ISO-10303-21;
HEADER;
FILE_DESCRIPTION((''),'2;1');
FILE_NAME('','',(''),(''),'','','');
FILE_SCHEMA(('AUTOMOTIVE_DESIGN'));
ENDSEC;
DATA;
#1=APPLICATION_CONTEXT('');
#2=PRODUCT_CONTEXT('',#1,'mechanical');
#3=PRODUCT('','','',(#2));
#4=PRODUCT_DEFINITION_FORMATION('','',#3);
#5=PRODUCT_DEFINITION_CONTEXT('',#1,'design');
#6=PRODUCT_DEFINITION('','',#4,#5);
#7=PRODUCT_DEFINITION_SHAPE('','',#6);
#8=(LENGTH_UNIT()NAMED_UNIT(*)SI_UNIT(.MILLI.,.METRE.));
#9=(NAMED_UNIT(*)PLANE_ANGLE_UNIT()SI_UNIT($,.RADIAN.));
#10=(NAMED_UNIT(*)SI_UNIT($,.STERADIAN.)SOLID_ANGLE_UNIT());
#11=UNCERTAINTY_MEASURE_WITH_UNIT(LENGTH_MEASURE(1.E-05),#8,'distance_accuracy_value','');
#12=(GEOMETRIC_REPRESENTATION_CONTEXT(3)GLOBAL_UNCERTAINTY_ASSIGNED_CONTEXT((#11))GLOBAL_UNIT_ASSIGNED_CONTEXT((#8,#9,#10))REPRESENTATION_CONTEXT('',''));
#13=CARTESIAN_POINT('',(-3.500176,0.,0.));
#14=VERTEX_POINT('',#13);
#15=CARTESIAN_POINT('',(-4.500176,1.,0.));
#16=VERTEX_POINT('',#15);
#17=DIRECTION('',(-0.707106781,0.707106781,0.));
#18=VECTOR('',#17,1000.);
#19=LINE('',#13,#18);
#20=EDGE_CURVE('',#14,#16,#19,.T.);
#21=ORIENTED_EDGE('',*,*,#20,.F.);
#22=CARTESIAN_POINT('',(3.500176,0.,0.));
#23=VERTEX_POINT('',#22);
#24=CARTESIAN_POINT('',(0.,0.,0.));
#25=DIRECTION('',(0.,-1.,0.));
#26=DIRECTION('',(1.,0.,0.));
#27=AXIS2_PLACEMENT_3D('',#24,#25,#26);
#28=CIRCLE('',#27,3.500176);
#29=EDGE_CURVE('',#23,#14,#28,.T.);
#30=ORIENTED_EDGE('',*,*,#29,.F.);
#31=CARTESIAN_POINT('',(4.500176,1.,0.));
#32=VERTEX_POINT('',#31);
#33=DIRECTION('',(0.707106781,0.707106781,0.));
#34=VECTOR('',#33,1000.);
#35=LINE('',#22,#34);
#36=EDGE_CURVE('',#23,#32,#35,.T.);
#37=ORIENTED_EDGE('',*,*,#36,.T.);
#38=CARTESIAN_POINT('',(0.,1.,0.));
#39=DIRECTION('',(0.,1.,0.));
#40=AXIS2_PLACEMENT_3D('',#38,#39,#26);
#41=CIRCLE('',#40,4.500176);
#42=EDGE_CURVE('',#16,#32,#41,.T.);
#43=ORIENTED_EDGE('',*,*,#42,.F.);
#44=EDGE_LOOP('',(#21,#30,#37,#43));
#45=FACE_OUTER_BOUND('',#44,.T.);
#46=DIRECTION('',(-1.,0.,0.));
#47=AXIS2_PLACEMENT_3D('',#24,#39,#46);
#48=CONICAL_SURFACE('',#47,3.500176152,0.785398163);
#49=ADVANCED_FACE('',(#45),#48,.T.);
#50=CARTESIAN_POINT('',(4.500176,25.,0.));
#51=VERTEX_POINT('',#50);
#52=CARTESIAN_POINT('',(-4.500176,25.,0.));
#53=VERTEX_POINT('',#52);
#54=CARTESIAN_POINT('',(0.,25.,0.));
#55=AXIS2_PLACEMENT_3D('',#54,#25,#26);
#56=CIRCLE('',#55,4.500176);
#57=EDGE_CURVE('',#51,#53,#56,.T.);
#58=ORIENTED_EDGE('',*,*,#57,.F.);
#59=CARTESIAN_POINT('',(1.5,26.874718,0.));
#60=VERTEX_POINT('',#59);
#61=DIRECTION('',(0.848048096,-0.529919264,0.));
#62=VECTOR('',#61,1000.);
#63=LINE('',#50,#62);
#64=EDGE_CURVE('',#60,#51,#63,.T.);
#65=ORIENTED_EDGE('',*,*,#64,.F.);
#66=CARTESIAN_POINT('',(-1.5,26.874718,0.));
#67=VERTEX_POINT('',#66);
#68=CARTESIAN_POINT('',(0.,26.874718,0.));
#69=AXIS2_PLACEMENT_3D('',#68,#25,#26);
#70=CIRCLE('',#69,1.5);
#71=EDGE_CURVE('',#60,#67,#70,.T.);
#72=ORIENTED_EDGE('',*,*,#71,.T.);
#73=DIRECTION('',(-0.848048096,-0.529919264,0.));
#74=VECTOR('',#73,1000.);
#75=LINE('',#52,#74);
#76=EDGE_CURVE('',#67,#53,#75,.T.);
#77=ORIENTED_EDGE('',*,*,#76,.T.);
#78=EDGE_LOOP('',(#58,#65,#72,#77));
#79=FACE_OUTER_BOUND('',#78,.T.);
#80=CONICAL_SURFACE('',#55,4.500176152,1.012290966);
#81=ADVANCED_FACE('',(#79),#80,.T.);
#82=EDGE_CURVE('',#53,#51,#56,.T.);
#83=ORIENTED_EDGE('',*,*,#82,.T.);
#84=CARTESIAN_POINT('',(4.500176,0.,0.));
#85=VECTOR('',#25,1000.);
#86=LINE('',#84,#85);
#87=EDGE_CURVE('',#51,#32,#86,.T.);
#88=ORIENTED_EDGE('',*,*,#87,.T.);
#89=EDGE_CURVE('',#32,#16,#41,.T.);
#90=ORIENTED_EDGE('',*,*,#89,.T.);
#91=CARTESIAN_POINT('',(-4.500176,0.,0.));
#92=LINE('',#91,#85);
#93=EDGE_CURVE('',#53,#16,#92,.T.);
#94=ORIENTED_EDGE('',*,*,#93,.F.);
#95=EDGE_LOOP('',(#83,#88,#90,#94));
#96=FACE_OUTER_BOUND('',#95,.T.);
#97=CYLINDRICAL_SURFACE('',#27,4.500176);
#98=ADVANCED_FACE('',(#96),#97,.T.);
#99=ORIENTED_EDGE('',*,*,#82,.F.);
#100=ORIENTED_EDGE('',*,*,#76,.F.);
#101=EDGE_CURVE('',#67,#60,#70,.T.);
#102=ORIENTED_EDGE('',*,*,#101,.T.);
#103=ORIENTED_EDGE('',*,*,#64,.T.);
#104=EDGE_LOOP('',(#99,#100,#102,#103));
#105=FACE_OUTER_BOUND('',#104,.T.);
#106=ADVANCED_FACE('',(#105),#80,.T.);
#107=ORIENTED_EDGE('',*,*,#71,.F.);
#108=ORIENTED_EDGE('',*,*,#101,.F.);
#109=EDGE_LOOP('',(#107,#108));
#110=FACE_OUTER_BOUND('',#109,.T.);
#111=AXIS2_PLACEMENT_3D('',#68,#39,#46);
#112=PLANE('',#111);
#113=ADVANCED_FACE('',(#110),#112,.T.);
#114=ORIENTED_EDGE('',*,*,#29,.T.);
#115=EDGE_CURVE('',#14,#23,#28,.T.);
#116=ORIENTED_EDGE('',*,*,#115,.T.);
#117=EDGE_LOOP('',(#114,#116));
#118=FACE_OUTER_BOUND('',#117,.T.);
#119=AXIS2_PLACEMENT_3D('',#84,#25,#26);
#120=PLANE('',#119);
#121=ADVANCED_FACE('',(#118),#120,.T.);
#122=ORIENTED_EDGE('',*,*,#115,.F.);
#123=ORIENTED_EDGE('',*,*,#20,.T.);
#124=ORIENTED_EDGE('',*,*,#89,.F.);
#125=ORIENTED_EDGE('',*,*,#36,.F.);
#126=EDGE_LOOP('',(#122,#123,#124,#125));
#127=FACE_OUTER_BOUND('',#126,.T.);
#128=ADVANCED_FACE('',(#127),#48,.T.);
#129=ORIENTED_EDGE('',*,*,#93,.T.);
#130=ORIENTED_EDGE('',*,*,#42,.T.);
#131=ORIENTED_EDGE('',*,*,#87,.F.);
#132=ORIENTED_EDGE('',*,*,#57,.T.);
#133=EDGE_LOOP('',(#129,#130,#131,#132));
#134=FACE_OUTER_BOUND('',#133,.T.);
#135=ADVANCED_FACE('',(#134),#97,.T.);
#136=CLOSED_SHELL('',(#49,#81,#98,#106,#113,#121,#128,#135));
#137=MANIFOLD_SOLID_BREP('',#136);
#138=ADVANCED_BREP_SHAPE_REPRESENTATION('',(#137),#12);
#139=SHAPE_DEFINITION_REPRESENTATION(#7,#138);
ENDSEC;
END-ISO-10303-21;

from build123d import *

# Parameters (mm, degrees)
CHAMFER1_SIZE = 1


with BuildPart() as part:
    # Sketch1 → Revolve1 (revolve)
    with BuildSketch(Plane.XY):
        Polygon((0, 26.874718128), (1.5, 26.874718128), (4.500176152, 25), (4.500176152, 0), (0, 0), align=None)
    revolve(axis=Axis((0, 0, 0), (0, 1, 0)))

    # Chamfer1
    chamfer1_edges = [part.edges().sort_by_distance(p)[0] for p in [
        (-4.500176152, 0, 0),
    ]]
    chamfer(chamfer1_edges, length=CHAMFER1_SIZE)


solid = part.part
